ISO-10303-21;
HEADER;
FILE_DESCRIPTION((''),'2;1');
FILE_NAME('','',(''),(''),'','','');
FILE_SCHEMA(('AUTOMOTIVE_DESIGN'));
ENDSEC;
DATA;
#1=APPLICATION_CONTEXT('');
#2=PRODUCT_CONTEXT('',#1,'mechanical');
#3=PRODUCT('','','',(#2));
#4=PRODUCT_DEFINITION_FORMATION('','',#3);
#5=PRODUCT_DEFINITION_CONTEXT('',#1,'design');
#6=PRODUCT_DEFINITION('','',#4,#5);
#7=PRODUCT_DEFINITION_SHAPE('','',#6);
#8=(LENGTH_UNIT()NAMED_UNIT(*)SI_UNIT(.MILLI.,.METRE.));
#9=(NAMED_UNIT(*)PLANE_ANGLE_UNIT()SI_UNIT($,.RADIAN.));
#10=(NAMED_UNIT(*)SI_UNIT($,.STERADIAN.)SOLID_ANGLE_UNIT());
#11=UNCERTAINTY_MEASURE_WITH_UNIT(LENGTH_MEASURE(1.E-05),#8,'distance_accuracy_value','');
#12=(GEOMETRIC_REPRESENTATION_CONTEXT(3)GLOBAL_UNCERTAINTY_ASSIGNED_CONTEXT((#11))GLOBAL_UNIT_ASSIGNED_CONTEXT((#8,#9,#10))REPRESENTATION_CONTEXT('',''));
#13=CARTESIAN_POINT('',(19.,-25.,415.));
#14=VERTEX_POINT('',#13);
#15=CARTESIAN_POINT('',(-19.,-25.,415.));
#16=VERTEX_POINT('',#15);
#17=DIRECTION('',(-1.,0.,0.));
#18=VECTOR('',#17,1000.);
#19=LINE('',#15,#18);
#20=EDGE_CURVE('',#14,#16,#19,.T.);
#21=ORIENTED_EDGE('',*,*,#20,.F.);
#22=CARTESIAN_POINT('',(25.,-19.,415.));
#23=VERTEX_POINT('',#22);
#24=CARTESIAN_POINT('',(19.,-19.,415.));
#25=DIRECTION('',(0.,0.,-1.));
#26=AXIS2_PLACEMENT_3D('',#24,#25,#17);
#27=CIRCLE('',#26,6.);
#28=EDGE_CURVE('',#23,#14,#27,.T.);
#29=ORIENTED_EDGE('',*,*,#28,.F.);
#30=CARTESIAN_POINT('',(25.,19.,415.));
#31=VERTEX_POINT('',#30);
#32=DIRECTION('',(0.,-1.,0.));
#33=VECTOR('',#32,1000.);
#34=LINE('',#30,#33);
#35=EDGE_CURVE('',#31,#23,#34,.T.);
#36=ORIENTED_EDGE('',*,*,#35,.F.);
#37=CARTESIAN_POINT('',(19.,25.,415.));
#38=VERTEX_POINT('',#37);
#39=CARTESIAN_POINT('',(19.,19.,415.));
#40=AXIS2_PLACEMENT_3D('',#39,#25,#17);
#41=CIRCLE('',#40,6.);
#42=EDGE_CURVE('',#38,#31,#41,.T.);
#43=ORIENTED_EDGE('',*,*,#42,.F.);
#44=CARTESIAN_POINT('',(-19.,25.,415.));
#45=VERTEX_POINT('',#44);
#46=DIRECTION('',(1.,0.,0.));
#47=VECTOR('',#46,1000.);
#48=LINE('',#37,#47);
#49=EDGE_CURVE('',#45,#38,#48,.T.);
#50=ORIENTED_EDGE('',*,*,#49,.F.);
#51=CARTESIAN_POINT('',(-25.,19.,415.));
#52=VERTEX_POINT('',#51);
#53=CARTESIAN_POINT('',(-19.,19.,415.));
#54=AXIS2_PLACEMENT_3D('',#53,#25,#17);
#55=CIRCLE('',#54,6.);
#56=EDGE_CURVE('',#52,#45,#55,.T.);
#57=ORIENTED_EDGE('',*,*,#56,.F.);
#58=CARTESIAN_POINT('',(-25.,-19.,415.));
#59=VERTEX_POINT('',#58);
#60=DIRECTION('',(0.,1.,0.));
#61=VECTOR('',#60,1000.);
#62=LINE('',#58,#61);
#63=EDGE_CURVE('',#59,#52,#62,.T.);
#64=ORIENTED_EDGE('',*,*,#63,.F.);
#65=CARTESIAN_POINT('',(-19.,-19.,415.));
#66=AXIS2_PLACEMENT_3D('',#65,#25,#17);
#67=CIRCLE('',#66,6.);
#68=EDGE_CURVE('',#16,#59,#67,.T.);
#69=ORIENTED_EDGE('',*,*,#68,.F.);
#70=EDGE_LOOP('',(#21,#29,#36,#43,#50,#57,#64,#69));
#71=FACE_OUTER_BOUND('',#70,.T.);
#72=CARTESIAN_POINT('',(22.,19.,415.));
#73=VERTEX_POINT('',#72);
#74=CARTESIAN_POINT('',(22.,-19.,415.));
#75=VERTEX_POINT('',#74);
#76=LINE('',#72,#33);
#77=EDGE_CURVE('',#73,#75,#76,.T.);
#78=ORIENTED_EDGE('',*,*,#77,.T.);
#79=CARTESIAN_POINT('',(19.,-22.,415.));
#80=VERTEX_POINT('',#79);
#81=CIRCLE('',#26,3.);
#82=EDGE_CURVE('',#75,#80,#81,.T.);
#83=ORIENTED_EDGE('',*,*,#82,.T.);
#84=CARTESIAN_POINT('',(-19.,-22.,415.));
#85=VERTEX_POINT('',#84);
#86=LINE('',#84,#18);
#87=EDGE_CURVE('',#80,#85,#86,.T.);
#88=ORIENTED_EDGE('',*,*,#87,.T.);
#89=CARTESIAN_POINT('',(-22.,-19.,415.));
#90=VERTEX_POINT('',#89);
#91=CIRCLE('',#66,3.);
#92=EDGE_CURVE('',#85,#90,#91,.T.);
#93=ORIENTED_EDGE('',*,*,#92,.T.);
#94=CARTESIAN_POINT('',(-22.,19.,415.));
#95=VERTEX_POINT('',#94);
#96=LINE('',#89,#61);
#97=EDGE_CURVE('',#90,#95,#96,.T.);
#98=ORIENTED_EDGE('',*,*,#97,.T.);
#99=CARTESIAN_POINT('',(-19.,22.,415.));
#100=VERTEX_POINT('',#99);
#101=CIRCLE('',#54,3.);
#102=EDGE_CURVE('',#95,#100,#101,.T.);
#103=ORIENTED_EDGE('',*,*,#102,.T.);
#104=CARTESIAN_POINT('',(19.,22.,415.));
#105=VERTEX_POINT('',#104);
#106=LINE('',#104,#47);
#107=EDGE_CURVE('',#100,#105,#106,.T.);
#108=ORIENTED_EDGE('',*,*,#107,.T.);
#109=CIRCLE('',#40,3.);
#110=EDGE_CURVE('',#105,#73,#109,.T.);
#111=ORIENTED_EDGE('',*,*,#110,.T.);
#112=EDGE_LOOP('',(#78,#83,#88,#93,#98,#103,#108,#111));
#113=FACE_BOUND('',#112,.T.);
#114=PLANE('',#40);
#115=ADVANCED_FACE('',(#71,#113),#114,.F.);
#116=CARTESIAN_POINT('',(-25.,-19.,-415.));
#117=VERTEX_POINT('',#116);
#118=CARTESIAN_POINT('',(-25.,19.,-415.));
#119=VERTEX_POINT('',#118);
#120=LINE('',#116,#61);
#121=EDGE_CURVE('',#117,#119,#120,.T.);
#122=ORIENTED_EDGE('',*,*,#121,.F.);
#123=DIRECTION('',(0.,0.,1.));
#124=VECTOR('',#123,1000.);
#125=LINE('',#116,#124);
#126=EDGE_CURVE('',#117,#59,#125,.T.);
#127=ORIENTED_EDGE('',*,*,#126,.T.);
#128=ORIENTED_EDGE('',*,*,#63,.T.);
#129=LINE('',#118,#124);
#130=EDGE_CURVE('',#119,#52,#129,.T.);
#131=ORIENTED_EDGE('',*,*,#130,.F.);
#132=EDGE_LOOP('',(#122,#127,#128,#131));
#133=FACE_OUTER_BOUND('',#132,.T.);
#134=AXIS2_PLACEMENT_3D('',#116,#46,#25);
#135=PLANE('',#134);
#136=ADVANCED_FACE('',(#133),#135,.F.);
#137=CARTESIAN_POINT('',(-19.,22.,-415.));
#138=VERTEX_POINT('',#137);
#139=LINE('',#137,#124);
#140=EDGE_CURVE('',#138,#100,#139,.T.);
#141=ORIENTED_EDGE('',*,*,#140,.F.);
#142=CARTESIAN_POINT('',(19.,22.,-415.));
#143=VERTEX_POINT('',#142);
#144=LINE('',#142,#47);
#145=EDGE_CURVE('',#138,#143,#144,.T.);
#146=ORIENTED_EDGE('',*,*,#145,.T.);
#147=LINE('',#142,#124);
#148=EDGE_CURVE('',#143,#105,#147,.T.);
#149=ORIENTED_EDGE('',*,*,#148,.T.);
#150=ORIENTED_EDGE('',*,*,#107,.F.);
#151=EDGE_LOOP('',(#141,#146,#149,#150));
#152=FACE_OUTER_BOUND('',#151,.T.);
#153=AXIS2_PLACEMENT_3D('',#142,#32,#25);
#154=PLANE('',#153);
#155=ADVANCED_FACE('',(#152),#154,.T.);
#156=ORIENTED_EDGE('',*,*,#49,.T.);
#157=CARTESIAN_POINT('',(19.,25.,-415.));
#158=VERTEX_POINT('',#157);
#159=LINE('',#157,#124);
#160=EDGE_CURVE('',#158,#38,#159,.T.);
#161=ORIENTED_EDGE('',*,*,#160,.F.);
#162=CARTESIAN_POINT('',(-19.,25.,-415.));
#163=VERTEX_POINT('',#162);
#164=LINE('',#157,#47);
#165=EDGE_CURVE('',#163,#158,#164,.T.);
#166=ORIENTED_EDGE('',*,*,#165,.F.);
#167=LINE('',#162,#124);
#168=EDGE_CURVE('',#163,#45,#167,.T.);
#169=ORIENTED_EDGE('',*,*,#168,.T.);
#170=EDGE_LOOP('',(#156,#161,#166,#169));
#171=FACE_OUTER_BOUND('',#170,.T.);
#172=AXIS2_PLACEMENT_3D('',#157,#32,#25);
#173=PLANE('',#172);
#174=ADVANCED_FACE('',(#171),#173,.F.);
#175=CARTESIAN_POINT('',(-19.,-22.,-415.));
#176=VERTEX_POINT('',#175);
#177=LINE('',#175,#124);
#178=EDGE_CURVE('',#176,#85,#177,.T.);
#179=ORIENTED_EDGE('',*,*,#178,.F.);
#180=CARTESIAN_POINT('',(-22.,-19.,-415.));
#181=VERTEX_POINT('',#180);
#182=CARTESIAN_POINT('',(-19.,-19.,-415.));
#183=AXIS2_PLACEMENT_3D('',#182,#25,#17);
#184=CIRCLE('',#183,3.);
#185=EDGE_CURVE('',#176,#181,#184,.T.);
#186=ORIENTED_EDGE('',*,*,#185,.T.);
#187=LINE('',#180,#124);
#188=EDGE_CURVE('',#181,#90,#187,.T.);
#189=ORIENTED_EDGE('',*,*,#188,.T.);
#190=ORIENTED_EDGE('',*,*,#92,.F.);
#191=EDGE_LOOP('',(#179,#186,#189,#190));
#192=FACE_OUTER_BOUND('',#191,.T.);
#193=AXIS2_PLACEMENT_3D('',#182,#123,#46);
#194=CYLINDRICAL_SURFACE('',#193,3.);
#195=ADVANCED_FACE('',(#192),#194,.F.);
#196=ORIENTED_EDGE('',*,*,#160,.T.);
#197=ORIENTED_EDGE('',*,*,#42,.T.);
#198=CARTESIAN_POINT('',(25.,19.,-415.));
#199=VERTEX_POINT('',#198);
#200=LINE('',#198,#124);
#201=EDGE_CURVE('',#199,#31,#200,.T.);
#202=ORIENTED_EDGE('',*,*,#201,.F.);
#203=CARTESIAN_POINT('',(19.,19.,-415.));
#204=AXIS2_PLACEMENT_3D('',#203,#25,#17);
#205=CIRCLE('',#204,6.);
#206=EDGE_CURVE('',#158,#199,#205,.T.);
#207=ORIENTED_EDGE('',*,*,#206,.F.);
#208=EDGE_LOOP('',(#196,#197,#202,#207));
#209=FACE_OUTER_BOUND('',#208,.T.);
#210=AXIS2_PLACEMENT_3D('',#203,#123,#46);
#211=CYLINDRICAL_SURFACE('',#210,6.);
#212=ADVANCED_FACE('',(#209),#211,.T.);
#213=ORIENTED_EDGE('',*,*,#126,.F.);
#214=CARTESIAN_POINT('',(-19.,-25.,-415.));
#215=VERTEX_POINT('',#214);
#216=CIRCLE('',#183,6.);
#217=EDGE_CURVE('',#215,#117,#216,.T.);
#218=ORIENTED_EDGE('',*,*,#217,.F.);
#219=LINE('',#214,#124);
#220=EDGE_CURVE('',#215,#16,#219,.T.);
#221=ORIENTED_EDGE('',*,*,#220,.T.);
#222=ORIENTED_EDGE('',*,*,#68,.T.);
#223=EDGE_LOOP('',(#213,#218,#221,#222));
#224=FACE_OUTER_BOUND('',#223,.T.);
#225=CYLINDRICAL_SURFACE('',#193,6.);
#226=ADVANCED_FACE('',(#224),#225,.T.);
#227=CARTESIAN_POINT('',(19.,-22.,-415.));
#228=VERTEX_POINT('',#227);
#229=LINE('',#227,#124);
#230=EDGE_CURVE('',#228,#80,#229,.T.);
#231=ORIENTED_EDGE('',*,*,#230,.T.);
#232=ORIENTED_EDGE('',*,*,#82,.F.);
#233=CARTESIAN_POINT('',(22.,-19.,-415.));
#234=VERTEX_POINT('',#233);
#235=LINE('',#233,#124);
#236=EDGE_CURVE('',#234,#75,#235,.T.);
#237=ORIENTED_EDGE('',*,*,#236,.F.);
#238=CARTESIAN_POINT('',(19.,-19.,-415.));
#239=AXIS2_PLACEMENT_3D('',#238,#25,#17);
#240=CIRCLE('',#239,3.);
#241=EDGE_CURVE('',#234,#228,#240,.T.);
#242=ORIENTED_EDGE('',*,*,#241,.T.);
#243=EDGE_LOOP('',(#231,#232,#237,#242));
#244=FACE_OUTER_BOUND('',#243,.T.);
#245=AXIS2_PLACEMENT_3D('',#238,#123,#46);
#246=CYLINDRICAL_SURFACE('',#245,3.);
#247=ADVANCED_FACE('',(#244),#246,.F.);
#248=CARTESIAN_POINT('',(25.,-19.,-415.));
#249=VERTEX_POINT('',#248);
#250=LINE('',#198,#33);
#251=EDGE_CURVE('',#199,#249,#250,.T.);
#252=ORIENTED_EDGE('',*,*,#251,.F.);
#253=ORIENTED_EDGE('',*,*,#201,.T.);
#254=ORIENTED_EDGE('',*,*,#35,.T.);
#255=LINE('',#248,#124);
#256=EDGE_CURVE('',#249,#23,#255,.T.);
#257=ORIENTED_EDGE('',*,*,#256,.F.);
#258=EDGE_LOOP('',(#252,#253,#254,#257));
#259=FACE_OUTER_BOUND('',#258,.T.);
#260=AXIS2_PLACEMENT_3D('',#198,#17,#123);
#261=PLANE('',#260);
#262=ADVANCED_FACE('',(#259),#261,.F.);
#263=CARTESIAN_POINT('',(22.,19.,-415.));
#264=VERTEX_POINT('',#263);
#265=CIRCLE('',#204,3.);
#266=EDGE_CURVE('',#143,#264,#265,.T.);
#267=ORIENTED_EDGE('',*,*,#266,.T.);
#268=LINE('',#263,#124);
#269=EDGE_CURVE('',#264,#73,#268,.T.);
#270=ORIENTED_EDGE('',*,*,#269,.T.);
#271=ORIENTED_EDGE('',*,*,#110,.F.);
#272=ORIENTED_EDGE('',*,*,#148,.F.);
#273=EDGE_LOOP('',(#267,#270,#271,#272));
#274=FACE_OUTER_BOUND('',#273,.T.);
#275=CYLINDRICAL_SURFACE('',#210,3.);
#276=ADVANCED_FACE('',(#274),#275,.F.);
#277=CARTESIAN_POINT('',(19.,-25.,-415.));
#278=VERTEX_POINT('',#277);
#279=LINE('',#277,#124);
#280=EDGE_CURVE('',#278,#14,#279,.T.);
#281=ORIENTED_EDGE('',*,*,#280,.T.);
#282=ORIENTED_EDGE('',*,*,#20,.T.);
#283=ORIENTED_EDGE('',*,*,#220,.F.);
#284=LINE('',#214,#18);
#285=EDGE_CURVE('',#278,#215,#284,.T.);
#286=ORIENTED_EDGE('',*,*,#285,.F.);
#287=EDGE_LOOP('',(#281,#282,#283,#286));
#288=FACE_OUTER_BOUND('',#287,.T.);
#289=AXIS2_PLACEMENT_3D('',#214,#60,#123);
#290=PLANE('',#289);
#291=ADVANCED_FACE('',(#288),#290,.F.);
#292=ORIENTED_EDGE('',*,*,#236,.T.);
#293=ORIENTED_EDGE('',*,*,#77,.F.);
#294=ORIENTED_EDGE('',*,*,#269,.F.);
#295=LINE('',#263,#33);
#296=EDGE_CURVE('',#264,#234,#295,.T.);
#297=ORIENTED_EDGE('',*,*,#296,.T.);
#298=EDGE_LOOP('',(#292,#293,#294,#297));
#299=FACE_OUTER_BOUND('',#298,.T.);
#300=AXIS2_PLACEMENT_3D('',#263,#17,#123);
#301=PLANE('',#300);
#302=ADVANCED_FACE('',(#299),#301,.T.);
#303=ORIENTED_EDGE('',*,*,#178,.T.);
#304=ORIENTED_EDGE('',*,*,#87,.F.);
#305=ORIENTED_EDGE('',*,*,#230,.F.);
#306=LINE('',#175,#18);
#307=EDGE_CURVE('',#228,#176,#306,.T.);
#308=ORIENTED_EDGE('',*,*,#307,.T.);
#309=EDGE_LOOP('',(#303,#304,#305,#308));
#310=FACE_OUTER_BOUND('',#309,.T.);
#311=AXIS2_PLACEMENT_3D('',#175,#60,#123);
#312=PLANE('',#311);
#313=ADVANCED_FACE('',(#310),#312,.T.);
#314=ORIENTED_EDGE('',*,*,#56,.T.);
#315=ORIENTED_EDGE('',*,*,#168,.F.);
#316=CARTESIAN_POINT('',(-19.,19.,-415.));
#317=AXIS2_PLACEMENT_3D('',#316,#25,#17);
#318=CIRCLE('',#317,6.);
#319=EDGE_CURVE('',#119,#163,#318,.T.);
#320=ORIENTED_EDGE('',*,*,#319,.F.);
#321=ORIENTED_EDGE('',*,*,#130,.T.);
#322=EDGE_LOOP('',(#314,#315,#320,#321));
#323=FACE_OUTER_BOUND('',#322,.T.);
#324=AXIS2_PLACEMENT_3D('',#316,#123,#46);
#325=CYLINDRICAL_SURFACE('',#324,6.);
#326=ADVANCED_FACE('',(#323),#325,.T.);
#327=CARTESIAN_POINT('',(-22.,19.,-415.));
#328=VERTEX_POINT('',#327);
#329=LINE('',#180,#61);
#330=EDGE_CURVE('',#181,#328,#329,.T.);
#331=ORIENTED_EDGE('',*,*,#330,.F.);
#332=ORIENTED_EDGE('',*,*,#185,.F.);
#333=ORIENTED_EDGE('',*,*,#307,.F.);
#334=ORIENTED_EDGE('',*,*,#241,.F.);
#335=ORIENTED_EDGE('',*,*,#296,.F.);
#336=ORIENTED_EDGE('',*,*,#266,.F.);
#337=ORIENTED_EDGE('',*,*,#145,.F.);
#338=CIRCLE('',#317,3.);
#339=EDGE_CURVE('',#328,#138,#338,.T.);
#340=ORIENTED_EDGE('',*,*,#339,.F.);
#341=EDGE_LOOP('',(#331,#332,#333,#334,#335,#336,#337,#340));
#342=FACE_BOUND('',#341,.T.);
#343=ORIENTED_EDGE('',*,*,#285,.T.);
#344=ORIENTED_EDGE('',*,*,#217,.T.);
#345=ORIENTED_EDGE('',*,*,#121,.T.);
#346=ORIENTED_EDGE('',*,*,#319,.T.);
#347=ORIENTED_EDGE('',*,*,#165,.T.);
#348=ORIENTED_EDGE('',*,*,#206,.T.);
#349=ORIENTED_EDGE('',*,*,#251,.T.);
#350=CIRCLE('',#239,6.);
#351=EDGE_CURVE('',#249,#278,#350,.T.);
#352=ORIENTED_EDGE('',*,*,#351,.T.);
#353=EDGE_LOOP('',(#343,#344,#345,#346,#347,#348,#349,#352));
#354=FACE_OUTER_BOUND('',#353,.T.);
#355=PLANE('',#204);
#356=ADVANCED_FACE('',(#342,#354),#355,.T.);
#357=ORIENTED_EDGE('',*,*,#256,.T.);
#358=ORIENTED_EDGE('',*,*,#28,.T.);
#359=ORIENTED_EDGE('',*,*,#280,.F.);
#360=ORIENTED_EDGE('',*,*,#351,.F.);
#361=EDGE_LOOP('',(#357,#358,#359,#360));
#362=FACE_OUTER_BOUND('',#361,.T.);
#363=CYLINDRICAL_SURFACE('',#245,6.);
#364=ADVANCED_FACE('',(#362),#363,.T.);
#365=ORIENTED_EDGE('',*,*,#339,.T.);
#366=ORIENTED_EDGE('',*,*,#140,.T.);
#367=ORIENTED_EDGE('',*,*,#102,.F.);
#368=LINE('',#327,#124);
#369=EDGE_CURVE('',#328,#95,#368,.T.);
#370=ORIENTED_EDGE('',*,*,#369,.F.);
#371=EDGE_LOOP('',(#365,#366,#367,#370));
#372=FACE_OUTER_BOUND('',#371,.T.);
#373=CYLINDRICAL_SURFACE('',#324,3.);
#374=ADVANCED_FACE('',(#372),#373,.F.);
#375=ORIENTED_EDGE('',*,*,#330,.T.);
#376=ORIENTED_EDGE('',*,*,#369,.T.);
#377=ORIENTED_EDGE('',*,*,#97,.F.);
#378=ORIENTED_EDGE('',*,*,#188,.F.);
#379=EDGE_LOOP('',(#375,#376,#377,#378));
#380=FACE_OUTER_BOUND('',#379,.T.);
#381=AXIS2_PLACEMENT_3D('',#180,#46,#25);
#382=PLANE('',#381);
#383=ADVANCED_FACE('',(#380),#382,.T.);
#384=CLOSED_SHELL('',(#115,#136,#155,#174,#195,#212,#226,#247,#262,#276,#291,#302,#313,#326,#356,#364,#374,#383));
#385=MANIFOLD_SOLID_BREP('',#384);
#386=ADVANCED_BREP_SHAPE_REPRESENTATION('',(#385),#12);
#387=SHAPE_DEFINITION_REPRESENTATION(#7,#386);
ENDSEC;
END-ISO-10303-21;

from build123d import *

# Parameters (mm, degrees)
GB_6728_1986_050_X_50_X_3_1_DEPTH = 830


with BuildPart() as part:
    # Sketch1 → Gb／6728-1986方形空心型钢 050 X 50 X 3(1) (new body)
    with BuildSketch(Plane.YX.offset(-415)):
        with BuildLine():
            Line((-19, -25), (19, -25))
            ThreePointArc((19, -25), (23.242640687, -23.242640687), (25, -19))
            Line((25, -19), (25, 19))
            ThreePointArc((25, 19), (23.242640687, 23.242640687), (19, 25))
            Line((19, 25), (-19, 25))
            ThreePointArc((-19, 25), (-23.242640687, 23.242640687), (-25, 19))
            Line((-25, 19), (-25, -19))
            ThreePointArc((-25, -19), (-23.242640687, -23.242640687), (-19, -25))
        make_face()
        with BuildLine():
            Line((-19, -22), (19, -22))
            ThreePointArc((19, -22), (21.121320344, -21.121320344), (22, -19))
            Line((22, -19), (22, 19))
            ThreePointArc((22, 19), (21.121320344, 21.121320344), (19, 22))
            Line((19, 22), (-19, 22))
            ThreePointArc((-19, 22), (-21.121320344, 21.121320344), (-22, 19))
            Line((-22, 19), (-22, -19))
            ThreePointArc((-22, -19), (-21.121320344, -21.121320344), (-19, -22))
        make_face(mode=Mode.SUBTRACT)
    extrude(amount=GB_6728_1986_050_X_50_X_3_1_DEPTH)


solid = part.part
